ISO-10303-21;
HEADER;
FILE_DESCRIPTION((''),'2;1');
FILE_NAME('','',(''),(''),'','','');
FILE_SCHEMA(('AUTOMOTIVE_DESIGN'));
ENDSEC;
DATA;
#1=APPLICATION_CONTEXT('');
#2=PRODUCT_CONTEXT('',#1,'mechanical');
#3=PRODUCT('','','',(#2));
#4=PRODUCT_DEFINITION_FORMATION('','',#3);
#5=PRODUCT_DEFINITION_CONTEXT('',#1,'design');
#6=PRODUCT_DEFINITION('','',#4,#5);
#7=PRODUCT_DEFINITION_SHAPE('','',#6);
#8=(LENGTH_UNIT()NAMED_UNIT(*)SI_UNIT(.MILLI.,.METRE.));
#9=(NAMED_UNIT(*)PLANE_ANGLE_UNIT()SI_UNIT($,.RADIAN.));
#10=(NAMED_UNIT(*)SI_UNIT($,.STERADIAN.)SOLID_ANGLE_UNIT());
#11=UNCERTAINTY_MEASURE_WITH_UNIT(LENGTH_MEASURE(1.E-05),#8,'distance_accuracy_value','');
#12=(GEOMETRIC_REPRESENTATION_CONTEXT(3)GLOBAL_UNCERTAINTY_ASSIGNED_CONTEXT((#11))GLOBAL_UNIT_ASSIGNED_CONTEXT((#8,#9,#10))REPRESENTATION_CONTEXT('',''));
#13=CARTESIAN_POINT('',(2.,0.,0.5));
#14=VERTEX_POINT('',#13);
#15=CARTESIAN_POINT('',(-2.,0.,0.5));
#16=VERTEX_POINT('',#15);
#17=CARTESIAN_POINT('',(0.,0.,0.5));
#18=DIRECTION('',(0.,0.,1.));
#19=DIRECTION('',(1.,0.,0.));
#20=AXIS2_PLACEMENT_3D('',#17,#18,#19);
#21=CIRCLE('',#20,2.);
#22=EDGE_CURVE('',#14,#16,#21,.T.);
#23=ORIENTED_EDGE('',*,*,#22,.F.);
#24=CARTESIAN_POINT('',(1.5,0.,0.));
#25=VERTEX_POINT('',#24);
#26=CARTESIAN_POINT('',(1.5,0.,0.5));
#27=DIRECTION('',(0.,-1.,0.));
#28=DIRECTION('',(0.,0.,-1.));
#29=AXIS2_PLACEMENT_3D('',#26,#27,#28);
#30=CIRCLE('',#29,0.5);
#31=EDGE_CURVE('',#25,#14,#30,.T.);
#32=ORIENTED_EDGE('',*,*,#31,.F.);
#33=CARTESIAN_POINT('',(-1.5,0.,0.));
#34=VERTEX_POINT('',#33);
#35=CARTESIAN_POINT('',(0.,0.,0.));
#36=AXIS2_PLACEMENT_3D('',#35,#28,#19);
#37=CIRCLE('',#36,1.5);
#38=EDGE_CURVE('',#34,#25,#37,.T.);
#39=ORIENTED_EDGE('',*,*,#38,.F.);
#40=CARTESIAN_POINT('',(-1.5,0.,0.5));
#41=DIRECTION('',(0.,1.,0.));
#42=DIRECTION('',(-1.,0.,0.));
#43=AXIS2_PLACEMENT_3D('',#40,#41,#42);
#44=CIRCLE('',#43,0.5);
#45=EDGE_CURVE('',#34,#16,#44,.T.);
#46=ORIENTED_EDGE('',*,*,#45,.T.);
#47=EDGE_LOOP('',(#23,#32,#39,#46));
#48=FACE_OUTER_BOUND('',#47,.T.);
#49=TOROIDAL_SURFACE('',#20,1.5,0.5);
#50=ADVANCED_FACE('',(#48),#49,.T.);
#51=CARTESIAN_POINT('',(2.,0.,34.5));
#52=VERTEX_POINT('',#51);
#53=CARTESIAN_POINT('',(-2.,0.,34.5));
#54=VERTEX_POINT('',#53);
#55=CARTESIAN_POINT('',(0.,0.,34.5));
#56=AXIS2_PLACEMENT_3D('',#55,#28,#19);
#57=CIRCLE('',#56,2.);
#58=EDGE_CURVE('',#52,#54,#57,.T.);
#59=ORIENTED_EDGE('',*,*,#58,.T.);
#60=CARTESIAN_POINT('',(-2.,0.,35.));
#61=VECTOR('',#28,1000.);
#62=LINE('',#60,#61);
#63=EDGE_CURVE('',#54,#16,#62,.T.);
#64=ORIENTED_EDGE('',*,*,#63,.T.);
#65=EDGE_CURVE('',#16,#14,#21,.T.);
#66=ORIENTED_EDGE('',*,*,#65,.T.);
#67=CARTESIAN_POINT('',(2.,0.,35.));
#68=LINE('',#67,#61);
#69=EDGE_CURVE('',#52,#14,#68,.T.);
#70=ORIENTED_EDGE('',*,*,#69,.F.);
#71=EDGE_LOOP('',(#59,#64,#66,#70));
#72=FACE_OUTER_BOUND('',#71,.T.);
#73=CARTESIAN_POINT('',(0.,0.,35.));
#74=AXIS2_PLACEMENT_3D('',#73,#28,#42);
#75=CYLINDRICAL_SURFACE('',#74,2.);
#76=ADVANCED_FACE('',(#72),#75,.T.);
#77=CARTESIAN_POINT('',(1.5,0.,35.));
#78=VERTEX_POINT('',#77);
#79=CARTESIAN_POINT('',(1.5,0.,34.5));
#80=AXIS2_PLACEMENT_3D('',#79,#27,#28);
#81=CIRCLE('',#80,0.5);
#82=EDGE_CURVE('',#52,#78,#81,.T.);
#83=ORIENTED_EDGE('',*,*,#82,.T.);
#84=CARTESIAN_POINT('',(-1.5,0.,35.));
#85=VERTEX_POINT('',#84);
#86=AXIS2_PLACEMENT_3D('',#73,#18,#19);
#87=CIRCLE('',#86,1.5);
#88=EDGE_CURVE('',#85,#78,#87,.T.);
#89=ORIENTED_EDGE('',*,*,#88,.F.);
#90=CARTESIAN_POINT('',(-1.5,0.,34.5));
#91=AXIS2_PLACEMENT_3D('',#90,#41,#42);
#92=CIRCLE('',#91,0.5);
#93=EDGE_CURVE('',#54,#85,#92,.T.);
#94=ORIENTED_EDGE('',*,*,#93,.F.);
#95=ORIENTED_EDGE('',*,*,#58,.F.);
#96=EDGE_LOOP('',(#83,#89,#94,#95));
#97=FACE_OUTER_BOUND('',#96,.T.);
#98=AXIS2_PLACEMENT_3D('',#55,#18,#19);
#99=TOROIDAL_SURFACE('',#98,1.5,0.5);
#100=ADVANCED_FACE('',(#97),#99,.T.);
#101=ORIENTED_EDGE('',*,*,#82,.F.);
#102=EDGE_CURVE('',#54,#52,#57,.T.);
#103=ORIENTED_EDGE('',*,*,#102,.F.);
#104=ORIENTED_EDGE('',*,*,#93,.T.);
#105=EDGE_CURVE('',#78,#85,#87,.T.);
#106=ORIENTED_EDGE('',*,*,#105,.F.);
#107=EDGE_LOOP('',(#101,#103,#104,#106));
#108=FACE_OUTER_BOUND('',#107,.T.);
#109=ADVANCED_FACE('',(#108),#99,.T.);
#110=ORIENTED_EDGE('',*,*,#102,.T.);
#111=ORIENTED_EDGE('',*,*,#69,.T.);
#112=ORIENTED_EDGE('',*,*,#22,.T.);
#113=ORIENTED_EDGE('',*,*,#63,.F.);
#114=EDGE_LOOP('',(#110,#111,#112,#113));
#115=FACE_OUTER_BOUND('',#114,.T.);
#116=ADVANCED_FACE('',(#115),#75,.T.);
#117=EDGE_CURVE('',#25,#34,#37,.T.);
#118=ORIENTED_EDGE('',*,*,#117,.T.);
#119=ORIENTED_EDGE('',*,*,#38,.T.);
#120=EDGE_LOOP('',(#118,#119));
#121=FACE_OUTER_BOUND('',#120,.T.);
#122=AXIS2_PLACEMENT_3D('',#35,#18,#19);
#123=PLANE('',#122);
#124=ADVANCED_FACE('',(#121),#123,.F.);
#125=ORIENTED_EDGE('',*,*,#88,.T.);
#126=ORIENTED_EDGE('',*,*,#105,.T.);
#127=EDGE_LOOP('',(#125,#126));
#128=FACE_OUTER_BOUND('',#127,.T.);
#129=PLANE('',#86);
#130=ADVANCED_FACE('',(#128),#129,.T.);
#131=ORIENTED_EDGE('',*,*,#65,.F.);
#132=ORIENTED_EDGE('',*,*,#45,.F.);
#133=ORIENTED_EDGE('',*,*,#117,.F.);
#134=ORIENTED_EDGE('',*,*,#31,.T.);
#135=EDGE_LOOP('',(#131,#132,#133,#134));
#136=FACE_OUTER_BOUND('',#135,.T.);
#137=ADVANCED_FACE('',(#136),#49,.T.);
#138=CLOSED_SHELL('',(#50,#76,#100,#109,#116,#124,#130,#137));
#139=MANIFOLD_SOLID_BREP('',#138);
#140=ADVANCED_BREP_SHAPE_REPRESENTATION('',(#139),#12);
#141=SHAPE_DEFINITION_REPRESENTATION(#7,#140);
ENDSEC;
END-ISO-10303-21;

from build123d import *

# Parameters (mm, degrees)
SKETCH1_R           = 2
BOSS_EXTRUDE1_DEPTH = 35
FILLET1_R           = 0.5


with BuildPart() as part:
    # Sketch1 → Boss-Extrude1 (new body)
    with BuildSketch(Plane.XY):
        Circle(SKETCH1_R)
    extrude(amount=BOSS_EXTRUDE1_DEPTH)

    # Fillet1
    fillet1_edges = [part.edges().sort_by_distance(p)[0] for p in [
        (-2, 0, 0),
        (-2, 0, 35),
    ]]
    fillet(fillet1_edges, radius=FILLET1_R)


solid = part.part
